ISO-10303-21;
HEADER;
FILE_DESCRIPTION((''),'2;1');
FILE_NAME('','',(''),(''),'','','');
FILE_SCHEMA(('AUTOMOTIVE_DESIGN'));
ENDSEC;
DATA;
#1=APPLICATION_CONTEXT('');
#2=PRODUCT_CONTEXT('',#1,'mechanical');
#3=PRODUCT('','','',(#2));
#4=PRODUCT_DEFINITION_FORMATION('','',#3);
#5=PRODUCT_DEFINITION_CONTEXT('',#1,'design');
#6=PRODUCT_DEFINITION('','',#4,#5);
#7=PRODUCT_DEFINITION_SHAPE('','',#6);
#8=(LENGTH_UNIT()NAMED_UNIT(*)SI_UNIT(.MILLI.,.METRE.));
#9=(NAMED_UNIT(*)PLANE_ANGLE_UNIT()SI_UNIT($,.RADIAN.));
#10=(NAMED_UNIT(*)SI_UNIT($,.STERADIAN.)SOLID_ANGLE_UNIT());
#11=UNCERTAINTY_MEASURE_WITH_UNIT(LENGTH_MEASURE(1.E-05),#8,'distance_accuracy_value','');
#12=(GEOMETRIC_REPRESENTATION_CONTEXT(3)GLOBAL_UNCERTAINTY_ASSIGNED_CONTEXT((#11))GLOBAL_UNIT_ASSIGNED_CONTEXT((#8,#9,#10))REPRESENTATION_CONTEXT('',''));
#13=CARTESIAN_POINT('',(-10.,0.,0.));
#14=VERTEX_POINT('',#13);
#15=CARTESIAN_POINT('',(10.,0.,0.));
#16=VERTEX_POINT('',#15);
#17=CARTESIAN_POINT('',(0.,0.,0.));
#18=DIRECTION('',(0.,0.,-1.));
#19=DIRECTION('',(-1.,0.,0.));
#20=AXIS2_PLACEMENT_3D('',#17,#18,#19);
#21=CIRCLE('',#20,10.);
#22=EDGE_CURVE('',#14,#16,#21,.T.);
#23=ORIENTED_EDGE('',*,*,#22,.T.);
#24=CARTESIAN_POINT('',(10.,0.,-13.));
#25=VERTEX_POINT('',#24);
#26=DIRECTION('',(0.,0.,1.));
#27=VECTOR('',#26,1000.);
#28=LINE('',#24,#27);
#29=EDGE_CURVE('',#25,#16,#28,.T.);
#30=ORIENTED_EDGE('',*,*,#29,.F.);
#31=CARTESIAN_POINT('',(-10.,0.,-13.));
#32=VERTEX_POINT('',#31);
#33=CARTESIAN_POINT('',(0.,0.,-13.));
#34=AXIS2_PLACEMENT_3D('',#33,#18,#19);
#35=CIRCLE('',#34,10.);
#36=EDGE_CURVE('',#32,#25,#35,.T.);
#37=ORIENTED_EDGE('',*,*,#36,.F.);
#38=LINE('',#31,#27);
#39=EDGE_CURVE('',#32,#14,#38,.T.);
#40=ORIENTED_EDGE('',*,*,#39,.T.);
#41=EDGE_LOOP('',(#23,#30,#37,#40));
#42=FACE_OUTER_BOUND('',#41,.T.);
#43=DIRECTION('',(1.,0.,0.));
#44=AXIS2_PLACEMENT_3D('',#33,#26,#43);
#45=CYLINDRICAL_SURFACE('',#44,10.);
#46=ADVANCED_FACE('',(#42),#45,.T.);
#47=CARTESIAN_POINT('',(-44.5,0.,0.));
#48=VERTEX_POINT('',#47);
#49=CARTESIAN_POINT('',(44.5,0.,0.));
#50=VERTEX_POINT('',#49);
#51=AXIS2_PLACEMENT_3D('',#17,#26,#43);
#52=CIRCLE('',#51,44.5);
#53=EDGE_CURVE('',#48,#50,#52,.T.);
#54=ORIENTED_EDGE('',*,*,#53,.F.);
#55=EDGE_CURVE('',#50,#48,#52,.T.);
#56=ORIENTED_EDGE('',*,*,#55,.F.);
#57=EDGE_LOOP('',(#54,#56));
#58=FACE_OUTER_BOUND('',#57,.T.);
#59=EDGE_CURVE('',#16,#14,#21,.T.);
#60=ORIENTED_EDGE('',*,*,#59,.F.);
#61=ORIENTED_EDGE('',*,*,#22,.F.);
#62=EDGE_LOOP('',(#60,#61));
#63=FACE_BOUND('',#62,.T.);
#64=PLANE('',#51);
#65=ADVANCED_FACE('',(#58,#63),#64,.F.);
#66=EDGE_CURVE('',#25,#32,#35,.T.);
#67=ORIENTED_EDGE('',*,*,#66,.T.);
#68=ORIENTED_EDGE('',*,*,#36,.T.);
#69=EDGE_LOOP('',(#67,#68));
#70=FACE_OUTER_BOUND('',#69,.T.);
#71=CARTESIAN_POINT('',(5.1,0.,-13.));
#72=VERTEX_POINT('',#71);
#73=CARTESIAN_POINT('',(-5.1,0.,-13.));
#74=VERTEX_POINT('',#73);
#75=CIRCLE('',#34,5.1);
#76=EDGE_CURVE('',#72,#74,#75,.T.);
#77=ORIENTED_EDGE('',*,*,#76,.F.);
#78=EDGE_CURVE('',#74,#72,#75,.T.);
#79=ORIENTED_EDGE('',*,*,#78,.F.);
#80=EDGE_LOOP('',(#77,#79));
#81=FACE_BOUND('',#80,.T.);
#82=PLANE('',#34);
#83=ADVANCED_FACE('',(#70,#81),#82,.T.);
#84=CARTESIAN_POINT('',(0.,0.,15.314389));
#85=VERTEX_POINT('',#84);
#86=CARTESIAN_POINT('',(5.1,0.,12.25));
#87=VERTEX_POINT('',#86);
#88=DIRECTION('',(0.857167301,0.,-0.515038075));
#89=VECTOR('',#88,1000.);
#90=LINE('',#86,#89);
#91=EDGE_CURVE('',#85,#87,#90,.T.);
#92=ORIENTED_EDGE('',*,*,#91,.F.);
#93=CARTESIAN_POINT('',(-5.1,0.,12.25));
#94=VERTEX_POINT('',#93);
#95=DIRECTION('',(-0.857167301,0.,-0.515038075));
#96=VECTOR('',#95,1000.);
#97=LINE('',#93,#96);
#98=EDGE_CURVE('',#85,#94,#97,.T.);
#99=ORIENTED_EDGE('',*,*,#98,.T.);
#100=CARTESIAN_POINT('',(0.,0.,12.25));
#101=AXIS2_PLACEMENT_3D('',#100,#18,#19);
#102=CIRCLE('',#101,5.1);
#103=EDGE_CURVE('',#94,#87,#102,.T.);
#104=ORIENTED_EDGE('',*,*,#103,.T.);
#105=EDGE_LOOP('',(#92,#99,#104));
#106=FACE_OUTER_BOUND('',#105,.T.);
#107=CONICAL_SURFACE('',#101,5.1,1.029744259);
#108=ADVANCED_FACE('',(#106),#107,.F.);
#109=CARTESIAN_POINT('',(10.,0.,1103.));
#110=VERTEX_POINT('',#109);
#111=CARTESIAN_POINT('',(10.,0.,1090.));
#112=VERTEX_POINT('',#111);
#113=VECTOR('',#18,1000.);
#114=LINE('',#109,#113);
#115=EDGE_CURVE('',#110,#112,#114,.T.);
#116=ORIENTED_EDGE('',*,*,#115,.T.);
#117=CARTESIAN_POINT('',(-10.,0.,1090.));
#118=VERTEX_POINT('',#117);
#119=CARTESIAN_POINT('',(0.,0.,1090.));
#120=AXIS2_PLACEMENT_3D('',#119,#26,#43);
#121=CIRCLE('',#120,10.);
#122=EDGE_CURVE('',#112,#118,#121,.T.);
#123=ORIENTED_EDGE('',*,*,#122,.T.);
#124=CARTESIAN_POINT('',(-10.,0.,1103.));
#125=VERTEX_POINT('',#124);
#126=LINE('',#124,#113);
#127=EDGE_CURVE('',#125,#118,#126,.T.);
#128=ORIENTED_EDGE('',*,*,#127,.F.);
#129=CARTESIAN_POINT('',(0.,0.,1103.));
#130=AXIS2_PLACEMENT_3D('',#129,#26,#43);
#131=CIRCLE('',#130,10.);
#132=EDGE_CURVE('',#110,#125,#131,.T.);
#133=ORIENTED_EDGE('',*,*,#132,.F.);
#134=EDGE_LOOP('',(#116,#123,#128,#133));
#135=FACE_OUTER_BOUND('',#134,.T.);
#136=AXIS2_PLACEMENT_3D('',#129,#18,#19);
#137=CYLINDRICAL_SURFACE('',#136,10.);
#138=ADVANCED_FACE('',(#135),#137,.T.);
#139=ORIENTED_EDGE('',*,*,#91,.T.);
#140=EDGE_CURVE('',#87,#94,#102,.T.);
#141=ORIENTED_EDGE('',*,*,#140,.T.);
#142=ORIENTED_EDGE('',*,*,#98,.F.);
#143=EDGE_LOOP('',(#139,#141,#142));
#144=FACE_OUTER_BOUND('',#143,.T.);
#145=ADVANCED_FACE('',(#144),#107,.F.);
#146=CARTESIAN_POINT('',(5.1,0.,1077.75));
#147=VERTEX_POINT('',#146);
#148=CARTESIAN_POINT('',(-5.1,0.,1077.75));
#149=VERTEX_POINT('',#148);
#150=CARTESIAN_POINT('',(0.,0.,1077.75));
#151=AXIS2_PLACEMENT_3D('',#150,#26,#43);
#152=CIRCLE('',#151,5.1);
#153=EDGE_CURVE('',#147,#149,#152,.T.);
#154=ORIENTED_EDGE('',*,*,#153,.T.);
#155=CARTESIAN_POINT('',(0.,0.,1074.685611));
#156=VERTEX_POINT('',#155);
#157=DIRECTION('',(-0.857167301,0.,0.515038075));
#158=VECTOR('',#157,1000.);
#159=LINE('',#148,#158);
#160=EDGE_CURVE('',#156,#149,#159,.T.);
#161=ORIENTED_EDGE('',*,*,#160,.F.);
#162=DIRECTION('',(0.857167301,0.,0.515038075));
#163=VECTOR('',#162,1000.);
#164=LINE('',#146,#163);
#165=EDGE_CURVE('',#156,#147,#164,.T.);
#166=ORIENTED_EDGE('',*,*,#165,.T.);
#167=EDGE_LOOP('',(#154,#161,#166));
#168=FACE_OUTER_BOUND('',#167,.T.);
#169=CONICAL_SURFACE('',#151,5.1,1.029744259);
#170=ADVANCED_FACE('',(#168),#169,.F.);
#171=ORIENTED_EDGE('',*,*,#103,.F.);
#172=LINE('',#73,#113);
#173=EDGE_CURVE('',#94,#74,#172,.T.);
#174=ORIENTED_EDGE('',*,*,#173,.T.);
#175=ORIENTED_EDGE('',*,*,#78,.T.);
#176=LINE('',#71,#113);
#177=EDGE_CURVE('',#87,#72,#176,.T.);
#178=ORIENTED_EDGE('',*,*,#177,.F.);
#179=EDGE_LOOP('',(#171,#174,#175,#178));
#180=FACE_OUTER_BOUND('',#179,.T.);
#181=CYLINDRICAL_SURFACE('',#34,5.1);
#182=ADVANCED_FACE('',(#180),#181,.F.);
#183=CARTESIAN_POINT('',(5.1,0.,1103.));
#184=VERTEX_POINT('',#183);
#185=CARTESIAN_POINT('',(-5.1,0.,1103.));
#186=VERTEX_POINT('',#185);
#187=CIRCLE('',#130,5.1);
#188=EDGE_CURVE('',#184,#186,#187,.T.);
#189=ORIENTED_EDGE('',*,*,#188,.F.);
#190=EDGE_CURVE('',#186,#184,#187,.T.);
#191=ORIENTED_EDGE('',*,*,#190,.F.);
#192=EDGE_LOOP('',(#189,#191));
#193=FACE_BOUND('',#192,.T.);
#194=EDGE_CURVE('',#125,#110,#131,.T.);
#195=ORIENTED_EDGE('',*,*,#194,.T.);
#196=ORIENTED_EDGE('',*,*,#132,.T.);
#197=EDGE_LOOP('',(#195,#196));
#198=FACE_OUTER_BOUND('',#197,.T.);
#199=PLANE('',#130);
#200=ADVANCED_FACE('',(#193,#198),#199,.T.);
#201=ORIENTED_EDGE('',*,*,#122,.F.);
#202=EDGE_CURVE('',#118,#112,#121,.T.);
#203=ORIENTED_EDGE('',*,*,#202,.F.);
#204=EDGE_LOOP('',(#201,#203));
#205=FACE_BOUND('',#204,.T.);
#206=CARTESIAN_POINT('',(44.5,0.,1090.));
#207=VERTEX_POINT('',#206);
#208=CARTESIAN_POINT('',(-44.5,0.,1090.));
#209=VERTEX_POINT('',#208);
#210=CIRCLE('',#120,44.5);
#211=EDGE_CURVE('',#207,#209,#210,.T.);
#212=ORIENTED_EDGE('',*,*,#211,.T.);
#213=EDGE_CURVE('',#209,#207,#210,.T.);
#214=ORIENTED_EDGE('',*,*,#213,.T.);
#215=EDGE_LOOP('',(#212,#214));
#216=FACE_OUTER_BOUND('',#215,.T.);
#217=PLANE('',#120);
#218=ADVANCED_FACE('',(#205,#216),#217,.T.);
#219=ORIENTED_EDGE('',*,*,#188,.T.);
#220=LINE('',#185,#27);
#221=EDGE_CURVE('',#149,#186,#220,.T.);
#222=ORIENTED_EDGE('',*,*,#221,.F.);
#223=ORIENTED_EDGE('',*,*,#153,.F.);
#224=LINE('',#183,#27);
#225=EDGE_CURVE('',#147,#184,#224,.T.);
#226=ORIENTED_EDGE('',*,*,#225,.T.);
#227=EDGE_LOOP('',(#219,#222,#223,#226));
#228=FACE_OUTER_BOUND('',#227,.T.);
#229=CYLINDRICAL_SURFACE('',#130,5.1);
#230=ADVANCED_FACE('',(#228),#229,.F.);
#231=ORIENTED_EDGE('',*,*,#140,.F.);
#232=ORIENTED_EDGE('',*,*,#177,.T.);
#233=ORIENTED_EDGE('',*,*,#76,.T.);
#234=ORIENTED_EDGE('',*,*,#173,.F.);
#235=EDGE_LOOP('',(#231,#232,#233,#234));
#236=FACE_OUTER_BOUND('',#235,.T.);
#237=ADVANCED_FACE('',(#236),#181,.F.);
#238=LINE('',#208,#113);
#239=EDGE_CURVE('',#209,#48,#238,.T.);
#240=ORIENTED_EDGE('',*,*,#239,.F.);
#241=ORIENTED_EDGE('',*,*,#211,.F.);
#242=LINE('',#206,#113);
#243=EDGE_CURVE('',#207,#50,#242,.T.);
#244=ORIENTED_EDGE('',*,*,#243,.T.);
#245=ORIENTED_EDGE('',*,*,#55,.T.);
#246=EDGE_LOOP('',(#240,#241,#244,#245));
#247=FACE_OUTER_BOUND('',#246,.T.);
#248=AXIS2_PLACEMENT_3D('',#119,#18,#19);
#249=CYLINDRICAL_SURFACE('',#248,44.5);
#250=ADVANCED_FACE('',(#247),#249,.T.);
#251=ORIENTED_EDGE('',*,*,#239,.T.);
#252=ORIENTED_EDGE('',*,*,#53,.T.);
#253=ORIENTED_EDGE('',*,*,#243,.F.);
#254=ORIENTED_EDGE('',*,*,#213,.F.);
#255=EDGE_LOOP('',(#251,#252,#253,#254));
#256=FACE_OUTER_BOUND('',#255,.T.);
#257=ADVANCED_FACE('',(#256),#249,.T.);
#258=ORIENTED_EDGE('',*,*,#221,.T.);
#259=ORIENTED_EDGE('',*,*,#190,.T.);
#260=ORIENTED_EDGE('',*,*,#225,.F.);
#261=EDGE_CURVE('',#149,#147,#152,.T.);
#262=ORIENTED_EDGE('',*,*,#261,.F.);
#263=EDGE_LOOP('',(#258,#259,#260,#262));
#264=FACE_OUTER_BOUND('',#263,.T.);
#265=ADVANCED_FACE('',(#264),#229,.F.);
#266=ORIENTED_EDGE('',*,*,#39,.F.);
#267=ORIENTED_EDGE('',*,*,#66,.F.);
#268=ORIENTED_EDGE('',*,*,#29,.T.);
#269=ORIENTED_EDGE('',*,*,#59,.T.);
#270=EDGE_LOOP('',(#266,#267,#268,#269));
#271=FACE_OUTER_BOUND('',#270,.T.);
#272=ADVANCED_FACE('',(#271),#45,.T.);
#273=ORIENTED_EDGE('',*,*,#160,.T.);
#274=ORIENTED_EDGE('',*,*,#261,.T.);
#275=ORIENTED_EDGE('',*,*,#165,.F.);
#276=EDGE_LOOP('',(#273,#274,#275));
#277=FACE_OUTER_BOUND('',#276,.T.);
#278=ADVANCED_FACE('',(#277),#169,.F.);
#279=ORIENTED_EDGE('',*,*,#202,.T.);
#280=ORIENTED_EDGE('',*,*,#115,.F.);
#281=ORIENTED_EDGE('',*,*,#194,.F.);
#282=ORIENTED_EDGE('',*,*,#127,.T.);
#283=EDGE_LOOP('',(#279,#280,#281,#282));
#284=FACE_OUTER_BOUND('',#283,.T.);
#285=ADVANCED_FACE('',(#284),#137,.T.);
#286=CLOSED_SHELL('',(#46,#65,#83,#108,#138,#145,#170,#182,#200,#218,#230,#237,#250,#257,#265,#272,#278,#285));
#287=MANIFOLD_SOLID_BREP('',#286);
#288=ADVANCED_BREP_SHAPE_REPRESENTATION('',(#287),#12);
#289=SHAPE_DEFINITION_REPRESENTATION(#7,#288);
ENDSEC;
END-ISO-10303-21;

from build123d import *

# Parameters (mm, degrees)
SKETCH1_R              = 44.5
BOSS_EXTRUDE1_DEPTH    = 1090
SKETCH2_R              = 10
BOSS_EXTRUDE2_DEPTH    = 13
BOSS_EXTRUDE3_START    = 13
SKETCH3_R              = 10
BOSS_EXTRUDE3_DEPTH    = 13
M12_TAPPED_HOLE1_D     = 10.2
M12_TAPPED_HOLE1_DEPTH = 25.25
M12_TAPPED_HOLE1_TIP   = 3.064389157
M12_TAPPED_HOLE2_D     = 10.2
M12_TAPPED_HOLE2_DEPTH = 25.25
M12_TAPPED_HOLE2_TIP   = 3.064389157


with BuildPart() as part:
    # Sketch1 → Boss-Extrude1 (new body)
    with BuildSketch(Plane.XY):
        Circle(SKETCH1_R)
    extrude(amount=BOSS_EXTRUDE1_DEPTH)

    # Sketch2 → Boss-Extrude2 (add)
    with BuildSketch(Plane.XY.offset(1090)):
        with Locations(Location((0, 0, 0), (0, 0, 180))):
            Circle(SKETCH2_R)
    extrude(amount=BOSS_EXTRUDE2_DEPTH)

    # Sketch3 → Boss-Extrude3 (add)
    with BuildSketch(Plane(origin=(0, 0, 0), x_dir=(-1, 0, 0), z_dir=(0, 0, -1)).offset(BOSS_EXTRUDE3_START)):
        Circle(SKETCH3_R)
    extrude(amount=-BOSS_EXTRUDE3_DEPTH)

    # M12 Tapped Hole1
    with Locations(Plane(origin=(0, 0, -13), x_dir=(-1, 0, 0), z_dir=(0, 0, -1))):
        with Locations((0, 0)):
            Hole(M12_TAPPED_HOLE1_D / 2, depth=M12_TAPPED_HOLE1_DEPTH)
            with Locations((0, 0, -(M12_TAPPED_HOLE1_DEPTH + M12_TAPPED_HOLE1_TIP / 2))):  # 118° drill point
                Cone(0, M12_TAPPED_HOLE1_D / 2, M12_TAPPED_HOLE1_TIP, mode=Mode.SUBTRACT)

    # M12 Tapped Hole2
    with Locations(Plane.XY.offset(1103)):
        with Locations((0, 0)):
            Hole(M12_TAPPED_HOLE2_D / 2, depth=M12_TAPPED_HOLE2_DEPTH)
            with Locations((0, 0, -(M12_TAPPED_HOLE2_DEPTH + M12_TAPPED_HOLE2_TIP / 2))):  # 118° drill point
                Cone(0, M12_TAPPED_HOLE2_D / 2, M12_TAPPED_HOLE2_TIP, mode=Mode.SUBTRACT)


solid = part.part
